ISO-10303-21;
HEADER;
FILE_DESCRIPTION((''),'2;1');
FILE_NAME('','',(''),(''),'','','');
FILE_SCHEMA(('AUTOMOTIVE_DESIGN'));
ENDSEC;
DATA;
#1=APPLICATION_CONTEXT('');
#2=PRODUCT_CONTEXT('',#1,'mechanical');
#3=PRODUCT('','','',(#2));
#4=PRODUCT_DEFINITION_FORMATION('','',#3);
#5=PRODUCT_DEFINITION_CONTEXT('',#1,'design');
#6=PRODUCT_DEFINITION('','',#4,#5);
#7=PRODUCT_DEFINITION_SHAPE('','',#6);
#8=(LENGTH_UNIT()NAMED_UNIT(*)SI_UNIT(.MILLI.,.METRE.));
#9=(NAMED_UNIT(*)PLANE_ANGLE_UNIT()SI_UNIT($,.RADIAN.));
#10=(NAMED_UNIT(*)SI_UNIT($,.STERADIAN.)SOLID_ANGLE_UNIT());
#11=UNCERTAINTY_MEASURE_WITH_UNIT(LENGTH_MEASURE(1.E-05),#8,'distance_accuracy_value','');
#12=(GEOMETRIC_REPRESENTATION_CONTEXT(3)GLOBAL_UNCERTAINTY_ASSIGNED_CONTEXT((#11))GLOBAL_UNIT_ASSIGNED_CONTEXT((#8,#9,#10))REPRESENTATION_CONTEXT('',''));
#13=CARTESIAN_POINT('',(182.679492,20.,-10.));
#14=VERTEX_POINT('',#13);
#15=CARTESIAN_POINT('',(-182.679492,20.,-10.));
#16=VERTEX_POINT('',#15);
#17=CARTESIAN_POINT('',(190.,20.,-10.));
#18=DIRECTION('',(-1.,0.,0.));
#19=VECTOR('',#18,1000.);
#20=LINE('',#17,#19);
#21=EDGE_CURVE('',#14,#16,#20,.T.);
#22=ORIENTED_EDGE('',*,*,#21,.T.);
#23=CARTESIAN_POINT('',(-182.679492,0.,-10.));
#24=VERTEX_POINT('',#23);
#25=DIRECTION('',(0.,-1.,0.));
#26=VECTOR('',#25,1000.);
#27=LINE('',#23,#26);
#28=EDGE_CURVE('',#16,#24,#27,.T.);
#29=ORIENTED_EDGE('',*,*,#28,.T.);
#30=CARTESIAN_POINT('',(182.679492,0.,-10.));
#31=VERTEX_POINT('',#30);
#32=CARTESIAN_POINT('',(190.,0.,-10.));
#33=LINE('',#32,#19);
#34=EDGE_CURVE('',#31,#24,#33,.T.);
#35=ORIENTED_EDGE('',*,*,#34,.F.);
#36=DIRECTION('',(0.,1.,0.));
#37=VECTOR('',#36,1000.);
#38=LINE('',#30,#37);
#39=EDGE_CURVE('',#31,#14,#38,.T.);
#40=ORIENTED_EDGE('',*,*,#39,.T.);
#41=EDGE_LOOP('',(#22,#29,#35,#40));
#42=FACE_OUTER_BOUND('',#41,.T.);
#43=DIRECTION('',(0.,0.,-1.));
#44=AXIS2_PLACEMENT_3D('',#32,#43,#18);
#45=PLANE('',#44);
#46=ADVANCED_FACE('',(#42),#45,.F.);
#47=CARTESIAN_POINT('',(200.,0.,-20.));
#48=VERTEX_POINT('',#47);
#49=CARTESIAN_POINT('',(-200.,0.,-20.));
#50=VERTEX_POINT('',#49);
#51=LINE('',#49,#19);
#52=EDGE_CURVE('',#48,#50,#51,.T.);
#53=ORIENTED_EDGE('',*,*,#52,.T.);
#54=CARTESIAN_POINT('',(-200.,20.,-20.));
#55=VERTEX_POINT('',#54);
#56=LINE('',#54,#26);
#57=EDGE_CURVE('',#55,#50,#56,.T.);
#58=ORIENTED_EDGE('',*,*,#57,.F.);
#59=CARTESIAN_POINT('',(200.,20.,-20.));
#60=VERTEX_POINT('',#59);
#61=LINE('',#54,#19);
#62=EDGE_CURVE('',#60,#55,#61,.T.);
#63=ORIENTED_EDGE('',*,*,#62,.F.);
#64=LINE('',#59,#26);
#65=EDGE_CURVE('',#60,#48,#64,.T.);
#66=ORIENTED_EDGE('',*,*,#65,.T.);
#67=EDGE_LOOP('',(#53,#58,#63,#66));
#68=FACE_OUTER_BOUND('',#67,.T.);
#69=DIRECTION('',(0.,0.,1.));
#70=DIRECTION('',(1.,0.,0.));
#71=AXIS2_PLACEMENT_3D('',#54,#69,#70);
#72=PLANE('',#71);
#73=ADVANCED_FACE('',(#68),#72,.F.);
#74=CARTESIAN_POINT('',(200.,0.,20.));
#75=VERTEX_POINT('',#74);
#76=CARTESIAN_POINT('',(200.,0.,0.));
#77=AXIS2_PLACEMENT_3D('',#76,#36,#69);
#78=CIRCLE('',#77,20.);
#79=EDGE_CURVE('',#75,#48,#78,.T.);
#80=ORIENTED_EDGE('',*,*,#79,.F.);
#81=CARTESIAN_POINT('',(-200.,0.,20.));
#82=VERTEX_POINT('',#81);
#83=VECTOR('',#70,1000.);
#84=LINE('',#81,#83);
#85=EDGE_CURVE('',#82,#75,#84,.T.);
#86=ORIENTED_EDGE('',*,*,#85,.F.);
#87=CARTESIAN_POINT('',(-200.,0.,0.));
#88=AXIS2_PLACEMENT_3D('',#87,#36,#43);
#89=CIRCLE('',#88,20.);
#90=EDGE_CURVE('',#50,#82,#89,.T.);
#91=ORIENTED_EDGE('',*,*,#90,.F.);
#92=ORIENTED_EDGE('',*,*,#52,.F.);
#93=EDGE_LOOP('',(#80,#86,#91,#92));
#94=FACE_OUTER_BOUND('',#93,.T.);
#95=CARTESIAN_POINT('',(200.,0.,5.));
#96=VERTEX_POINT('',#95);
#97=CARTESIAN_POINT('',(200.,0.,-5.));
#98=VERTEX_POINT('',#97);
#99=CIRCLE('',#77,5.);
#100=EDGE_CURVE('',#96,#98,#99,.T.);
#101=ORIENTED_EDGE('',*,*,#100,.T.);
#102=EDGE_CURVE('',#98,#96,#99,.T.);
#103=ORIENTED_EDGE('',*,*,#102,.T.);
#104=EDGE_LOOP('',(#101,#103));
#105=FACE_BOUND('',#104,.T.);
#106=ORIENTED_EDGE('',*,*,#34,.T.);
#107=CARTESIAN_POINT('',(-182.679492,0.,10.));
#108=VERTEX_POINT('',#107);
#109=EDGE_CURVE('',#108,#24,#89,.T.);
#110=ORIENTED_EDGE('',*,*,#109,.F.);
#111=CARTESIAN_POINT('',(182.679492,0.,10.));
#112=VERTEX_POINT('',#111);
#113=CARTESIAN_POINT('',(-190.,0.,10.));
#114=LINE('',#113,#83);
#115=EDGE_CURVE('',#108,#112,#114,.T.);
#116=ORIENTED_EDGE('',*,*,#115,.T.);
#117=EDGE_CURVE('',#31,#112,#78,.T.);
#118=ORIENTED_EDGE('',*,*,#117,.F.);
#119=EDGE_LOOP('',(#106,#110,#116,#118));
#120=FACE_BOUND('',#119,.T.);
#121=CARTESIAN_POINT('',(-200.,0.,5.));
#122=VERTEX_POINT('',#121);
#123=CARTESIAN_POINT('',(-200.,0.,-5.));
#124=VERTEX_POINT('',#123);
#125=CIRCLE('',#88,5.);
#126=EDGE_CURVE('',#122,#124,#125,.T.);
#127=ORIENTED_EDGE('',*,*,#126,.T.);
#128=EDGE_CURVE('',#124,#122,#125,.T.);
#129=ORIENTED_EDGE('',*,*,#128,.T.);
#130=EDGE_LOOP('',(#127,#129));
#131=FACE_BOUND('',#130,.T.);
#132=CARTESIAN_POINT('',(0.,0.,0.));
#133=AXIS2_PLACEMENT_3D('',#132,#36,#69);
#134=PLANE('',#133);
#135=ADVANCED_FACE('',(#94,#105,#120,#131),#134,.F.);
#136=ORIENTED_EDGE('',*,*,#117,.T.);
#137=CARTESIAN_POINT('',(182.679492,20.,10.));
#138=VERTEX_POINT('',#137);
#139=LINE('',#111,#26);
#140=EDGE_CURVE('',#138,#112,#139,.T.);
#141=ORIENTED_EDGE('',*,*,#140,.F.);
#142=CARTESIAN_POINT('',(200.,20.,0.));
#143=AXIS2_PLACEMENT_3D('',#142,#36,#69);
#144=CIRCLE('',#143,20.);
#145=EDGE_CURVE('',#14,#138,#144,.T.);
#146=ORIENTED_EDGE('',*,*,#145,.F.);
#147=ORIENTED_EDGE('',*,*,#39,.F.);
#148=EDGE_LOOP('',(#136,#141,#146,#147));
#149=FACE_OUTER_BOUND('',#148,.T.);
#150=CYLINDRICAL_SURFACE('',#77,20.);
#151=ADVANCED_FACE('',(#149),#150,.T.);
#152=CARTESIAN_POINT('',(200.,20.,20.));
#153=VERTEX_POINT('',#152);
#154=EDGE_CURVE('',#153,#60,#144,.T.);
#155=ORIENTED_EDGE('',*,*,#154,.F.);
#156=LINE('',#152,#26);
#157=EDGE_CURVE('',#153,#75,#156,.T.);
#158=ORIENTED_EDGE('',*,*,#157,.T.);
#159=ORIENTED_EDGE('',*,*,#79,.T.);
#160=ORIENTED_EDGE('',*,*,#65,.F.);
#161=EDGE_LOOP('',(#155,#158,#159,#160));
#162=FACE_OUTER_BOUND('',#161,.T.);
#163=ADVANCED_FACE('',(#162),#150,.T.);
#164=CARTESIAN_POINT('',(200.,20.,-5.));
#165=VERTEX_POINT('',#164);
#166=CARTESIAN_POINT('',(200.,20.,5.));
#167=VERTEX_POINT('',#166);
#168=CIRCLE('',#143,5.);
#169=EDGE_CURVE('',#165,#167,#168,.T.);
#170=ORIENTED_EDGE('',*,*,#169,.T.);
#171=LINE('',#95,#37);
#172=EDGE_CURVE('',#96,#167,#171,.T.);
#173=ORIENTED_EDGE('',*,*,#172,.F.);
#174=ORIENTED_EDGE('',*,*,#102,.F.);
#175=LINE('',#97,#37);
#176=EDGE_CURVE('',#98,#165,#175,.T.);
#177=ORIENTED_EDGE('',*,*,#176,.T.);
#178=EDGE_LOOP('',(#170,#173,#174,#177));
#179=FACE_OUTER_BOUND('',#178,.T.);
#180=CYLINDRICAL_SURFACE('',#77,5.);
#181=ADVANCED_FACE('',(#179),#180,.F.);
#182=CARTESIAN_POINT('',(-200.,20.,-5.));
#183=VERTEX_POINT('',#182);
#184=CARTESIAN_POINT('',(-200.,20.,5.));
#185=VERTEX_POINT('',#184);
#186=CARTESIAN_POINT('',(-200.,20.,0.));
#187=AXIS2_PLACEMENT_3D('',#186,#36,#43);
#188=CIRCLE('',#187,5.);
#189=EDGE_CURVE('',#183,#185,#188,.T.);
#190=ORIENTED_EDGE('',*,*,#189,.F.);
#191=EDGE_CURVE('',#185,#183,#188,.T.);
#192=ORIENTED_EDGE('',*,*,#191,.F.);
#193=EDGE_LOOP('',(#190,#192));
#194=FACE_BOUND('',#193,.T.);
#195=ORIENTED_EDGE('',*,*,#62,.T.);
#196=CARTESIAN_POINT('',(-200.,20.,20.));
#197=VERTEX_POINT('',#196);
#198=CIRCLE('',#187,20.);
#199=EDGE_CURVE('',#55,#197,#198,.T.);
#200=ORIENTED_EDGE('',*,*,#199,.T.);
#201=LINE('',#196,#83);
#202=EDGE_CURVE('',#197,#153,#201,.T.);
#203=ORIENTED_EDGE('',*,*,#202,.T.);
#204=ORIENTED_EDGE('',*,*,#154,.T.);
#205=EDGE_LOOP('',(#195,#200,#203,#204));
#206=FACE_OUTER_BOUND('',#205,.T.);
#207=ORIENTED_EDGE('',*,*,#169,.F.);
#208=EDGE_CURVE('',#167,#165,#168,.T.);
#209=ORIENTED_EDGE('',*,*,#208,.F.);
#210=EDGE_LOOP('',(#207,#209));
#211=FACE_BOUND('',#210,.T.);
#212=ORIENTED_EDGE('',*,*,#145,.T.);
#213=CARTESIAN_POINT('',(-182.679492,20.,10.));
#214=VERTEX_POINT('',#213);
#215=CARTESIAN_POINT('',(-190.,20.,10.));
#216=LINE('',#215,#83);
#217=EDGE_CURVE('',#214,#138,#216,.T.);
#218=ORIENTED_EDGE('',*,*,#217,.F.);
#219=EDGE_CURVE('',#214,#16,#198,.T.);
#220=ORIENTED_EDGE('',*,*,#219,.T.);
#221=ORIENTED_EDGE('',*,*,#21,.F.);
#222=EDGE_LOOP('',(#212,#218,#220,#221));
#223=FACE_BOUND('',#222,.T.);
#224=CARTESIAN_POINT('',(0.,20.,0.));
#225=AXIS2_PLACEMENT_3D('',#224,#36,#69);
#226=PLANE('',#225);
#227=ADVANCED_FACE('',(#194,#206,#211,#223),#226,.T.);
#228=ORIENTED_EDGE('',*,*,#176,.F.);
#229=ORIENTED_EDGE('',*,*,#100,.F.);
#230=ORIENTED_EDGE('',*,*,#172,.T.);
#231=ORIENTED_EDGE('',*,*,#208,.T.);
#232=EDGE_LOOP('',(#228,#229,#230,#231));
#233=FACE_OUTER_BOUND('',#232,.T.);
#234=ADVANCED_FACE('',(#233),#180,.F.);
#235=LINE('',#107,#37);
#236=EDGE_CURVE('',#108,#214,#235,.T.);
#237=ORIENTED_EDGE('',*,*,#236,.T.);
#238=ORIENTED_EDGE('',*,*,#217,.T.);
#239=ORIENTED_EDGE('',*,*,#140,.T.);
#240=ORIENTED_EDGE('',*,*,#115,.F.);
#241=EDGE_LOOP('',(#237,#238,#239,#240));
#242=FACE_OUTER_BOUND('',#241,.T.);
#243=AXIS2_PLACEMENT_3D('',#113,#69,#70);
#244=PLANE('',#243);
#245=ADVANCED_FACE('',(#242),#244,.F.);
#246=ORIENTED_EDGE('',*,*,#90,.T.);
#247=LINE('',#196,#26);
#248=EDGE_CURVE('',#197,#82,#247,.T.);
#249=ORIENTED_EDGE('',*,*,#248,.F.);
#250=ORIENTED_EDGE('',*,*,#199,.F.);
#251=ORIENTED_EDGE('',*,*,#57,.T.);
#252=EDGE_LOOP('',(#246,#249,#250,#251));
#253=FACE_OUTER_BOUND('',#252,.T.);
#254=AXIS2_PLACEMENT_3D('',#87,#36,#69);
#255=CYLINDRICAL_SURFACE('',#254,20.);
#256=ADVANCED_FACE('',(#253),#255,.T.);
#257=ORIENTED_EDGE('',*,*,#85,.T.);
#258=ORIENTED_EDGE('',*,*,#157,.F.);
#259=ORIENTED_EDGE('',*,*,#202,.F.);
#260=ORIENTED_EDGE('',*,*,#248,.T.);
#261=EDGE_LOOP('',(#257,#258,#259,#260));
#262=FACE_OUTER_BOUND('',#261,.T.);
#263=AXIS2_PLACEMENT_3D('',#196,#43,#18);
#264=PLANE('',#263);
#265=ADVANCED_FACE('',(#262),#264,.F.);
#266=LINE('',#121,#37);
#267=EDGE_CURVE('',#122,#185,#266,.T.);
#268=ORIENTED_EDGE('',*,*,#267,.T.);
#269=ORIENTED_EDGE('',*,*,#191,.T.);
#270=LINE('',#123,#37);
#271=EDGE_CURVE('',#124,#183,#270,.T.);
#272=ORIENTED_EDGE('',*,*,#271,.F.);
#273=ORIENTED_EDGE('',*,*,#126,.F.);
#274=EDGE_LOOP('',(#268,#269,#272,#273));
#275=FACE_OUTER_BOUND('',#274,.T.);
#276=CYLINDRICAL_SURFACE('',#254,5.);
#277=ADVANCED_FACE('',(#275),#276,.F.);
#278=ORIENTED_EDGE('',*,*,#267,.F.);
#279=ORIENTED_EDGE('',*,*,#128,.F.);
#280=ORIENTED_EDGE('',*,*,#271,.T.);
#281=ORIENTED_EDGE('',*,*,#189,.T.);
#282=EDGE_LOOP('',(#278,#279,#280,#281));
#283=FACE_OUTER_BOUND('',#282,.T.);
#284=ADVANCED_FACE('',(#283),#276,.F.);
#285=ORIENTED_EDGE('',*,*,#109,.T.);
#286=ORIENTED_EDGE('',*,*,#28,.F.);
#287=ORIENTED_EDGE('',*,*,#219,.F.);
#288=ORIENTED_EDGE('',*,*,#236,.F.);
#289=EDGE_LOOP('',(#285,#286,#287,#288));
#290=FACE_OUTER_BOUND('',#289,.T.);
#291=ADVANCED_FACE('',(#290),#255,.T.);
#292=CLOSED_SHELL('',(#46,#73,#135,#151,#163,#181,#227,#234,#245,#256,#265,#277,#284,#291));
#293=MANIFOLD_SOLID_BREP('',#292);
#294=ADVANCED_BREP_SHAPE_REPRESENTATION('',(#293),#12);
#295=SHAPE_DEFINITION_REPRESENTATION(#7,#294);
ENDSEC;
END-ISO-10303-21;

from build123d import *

# Parameters (mm, degrees)
SKETCH1_W           = 400
SKETCH1_H           = 40
BOSS_EXTRUDE1_DEPTH = 20
SKETCH2_W           = 380
SKETCH2_H           = 20
CUT_EXTRUDE1_DEPTH  = 202.990098767
SKETCH4_R           = 20
BOSS_EXTRUDE2_DEPTH = 20
SKETCH6_R           = 5
CUT_EXTRUDE2_DEPTH  = 222.810730128


with BuildPart() as part:
    # Sketch1 → Boss-Extrude1 (new body)
    with BuildSketch(Plane(origin=(0, 0, 0), x_dir=(1, 0, 0), z_dir=(0, 1, 0))):
        Rectangle(SKETCH1_W, SKETCH1_H)
    extrude(amount=BOSS_EXTRUDE1_DEPTH)

    # Sketch2 → Cut-Extrude1 (cut, through all)
    with BuildSketch(Plane(origin=(0, 20, 0), x_dir=(1, 0, 0), z_dir=(0, 1, 0))):
        Rectangle(SKETCH2_W, SKETCH2_H)
    extrude(amount=-CUT_EXTRUDE1_DEPTH, mode=Mode.SUBTRACT)

    # Sketch4 → Boss-Extrude2 (add)
    with BuildSketch(Plane(origin=(0, 20, 0), x_dir=(1, 0, 0), z_dir=(0, 1, 0))):
        with Locations((200, 0)):
            Circle(SKETCH4_R)
        with Locations((-200, 0)):
            Circle(SKETCH4_R)
    extrude(amount=-BOSS_EXTRUDE2_DEPTH)

    # Sketch6 → Cut-Extrude2 (cut, through all)
    with BuildSketch(Plane(origin=(0, 20, 0), x_dir=(1, 0, 0), z_dir=(0, 1, 0))):
        with Locations(Location((200, 0, 0), (0, 0, 270))):
            Circle(SKETCH6_R)
        with Locations(Location((-200, 0, 0), (0, 0, 90))):
            Circle(SKETCH6_R)
    extrude(amount=-CUT_EXTRUDE2_DEPTH, mode=Mode.SUBTRACT)


solid = part.part
